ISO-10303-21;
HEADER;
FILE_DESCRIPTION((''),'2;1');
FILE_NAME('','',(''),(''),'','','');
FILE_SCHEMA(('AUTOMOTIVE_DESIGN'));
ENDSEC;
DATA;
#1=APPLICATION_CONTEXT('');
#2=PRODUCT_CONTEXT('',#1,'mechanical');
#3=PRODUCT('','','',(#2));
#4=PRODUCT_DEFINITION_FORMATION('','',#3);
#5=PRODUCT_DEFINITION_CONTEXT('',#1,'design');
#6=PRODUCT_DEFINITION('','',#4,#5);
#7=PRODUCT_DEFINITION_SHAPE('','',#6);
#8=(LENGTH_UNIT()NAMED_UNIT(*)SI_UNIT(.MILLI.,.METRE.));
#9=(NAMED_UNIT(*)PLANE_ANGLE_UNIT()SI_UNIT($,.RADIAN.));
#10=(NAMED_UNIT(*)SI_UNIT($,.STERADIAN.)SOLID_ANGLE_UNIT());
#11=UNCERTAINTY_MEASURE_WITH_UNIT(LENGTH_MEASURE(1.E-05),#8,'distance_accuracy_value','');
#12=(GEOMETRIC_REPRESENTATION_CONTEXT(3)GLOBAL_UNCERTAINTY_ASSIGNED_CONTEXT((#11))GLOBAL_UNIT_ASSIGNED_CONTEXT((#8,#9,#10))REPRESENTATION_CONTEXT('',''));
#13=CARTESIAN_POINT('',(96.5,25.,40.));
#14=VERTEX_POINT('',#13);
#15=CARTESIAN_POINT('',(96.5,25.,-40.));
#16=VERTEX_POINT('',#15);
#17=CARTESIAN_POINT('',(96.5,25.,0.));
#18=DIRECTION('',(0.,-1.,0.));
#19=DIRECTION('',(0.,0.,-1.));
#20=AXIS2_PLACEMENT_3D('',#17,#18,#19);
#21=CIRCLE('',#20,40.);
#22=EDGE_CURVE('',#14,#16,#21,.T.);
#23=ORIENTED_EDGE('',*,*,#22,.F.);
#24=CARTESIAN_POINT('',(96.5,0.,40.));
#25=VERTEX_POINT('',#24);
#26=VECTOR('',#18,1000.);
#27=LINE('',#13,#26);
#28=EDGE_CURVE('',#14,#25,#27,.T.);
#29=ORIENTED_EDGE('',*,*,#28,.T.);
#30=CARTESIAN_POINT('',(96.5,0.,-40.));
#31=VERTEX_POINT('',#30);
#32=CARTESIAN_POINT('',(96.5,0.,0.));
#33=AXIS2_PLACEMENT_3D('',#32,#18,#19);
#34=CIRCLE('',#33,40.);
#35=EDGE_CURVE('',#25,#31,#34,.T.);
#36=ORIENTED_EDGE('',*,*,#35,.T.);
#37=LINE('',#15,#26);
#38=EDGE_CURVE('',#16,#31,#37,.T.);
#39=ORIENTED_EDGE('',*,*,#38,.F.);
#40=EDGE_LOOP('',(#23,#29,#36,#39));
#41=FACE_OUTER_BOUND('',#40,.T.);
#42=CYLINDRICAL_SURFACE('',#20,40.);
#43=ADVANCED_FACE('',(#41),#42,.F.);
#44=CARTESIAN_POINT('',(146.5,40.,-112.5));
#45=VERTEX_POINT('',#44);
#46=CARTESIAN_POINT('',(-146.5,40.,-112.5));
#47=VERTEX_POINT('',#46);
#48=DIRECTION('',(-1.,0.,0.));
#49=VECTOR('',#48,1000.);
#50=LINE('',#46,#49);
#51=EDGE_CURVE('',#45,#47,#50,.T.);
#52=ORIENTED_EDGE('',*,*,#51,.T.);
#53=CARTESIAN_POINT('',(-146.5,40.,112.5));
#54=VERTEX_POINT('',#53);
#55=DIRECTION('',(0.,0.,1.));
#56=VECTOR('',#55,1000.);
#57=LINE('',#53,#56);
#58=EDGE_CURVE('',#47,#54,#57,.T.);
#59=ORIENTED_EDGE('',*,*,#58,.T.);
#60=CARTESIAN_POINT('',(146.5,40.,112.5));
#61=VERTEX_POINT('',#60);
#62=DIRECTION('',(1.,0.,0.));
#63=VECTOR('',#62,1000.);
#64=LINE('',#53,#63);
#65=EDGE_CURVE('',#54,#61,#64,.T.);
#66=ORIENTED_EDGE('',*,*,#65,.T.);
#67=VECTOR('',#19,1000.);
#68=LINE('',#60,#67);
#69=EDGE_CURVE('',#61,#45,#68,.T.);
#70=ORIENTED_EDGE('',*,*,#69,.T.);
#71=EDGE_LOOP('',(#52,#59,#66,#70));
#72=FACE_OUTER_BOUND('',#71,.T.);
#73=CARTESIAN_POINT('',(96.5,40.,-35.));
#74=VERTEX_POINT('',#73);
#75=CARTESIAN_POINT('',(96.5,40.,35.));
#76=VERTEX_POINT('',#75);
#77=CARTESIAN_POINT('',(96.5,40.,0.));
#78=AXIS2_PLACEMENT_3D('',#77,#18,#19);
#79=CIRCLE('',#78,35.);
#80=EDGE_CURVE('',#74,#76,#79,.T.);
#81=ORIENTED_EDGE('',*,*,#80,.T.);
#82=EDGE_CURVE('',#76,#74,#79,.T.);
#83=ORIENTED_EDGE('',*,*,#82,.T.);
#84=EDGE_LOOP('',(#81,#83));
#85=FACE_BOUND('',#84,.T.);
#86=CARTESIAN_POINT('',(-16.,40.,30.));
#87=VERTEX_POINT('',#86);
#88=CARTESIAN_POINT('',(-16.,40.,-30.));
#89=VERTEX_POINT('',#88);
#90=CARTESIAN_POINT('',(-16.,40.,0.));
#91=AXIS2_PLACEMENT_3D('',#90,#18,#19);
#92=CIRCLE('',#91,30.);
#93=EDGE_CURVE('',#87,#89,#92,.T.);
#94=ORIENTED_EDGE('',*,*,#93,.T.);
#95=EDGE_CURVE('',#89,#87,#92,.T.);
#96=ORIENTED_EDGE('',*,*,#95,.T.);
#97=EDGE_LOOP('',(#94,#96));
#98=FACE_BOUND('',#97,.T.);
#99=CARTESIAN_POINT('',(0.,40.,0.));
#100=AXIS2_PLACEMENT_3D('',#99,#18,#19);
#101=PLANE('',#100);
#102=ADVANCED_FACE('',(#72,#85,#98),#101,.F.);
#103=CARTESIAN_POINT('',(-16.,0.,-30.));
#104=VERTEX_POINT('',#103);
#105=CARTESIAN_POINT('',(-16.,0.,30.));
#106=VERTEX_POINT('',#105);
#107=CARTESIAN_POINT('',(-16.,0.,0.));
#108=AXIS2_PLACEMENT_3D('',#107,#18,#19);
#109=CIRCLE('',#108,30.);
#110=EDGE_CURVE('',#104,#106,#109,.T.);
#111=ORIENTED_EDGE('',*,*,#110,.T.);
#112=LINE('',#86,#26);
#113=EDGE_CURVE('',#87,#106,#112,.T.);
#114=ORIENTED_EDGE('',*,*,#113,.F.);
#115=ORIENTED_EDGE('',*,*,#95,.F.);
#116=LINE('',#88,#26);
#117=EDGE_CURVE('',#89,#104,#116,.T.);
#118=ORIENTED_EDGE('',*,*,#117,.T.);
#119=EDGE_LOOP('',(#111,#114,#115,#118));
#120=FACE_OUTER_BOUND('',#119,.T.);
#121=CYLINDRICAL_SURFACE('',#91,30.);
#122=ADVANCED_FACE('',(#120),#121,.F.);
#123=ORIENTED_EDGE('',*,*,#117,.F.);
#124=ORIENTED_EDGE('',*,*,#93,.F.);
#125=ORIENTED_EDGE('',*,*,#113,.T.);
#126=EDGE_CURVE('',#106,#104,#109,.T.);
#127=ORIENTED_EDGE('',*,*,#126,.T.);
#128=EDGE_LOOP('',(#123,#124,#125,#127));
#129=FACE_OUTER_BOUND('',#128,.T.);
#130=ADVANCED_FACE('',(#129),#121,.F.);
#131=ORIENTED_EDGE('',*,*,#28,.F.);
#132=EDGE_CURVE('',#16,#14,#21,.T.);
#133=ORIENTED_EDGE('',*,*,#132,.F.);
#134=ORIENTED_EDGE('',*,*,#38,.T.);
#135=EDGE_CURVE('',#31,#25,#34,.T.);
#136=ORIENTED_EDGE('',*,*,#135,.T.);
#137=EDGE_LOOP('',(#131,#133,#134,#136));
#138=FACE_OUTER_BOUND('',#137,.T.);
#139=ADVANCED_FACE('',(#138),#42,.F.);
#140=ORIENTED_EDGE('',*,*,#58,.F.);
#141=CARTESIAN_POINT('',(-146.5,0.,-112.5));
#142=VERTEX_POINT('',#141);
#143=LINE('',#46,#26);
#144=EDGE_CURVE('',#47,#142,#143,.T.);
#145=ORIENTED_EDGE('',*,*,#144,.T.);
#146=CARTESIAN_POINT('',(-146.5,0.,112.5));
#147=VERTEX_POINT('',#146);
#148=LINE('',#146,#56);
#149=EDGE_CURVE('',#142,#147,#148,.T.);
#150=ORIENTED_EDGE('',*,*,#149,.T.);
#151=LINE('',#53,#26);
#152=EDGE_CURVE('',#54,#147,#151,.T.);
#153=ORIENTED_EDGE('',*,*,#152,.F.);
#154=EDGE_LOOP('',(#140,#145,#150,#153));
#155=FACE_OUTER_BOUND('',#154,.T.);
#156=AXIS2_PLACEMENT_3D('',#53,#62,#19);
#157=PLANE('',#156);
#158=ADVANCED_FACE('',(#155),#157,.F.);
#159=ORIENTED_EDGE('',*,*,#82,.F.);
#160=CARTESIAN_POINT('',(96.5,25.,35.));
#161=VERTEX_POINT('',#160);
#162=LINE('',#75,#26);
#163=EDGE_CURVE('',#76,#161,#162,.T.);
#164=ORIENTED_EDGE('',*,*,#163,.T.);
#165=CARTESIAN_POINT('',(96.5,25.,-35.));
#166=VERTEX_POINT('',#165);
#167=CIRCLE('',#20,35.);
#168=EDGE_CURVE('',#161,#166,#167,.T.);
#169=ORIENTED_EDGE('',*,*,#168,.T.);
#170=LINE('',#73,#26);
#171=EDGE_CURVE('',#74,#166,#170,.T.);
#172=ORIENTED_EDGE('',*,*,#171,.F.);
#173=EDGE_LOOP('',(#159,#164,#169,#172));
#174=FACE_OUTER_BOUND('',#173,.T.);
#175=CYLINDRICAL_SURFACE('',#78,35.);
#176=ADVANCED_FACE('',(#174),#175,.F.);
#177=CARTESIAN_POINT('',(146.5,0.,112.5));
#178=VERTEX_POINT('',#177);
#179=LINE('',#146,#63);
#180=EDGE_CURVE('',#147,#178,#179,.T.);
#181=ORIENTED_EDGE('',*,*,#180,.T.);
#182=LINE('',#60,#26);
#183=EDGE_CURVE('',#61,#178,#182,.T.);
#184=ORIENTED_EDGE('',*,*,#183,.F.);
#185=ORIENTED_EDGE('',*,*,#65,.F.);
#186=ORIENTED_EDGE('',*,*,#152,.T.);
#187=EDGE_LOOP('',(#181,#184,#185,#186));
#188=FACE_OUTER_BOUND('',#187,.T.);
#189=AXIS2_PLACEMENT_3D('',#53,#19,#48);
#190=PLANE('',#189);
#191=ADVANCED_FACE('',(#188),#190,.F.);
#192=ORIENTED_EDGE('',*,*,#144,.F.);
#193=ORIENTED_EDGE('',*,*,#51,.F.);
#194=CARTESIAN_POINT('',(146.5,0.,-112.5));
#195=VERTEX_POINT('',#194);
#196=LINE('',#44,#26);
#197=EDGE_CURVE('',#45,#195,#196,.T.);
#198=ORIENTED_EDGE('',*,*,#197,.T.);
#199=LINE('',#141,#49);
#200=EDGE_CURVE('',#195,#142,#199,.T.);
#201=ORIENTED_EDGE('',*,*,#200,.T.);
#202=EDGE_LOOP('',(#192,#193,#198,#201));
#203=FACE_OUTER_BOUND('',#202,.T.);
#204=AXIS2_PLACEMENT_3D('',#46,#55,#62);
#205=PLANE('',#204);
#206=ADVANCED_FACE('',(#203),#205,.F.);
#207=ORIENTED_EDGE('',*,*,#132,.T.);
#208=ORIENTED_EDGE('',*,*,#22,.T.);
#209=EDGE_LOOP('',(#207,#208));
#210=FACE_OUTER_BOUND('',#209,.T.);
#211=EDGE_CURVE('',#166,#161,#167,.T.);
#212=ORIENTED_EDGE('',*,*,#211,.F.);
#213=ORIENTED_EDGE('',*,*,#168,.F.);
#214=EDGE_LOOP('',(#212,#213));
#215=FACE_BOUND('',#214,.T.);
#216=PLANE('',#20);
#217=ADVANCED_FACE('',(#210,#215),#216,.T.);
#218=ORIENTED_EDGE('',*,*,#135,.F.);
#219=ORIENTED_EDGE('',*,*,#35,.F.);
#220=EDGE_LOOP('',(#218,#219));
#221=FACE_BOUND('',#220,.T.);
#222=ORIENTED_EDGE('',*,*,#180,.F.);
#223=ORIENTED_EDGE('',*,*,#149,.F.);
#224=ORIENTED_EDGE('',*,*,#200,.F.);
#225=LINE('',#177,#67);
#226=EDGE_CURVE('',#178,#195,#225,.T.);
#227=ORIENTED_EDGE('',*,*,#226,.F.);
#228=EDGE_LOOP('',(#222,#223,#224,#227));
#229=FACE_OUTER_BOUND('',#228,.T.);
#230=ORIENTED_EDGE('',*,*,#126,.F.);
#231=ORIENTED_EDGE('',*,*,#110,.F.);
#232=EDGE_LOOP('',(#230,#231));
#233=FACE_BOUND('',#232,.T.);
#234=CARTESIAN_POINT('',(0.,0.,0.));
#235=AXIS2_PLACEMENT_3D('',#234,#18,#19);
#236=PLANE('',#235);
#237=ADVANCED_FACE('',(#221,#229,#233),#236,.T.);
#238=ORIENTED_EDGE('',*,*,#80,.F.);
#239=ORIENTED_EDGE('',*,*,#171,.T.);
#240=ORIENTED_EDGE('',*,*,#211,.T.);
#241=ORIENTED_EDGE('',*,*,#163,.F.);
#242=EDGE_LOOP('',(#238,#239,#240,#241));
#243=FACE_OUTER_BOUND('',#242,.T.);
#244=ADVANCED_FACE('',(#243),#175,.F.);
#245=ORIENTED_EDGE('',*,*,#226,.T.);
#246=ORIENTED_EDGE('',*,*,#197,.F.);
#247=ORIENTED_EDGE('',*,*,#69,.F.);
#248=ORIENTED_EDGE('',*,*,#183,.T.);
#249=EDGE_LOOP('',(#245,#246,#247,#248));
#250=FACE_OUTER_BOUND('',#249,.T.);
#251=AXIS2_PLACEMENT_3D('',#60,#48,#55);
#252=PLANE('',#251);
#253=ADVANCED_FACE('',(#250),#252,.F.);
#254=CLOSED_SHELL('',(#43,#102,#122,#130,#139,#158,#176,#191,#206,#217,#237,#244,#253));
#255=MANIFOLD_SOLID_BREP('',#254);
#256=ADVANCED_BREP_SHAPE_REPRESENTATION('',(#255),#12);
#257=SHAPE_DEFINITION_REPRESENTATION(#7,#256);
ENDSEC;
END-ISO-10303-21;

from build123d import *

# Parameters (mm, degrees)
SKETCH_1_W          = 293
SKETCH_1_H          = 225
EXTRUDE_1_DEPTH     = 40
SKETCH_2_R          = 40
CUT_EXTRUDE_1_DEPTH = 25
SKETCH_3_R          = 30
CUT_EXTRUDE_2_DEPTH = 189.993386128
SKETCH_4_R          = 35
CUT_EXTRUDE_3_DEPTH = 189.993386128


with BuildPart() as part:
    # 草图1 → 凸台-拉伸1 (new body)
    with BuildSketch(Plane(origin=(0, 0, 0), x_dir=(1, 0, 0), z_dir=(0, 1, 0))):
        Rectangle(SKETCH_1_W, SKETCH_1_H)
    extrude(amount=EXTRUDE_1_DEPTH)

    # 草图2 → 切除-拉伸1 (cut)
    with BuildSketch(Plane.XZ):
        with Locations(Location((96.5, 0, 0), (0, 0, 270))):
            Circle(SKETCH_2_R)
    extrude(amount=-CUT_EXTRUDE_1_DEPTH, mode=Mode.SUBTRACT)

    # 草图3 → 切除-拉伸2 (cut, through all)
    with BuildSketch(Plane.XZ):
        with Locations(Location((-16, 0, 0), (0, 0, 270))):
            Circle(SKETCH_3_R)
    extrude(amount=-CUT_EXTRUDE_2_DEPTH, mode=Mode.SUBTRACT)

    # 草图4 → 切除-拉伸3 (cut, through all)
    with BuildSketch(Plane.XZ):
        with Locations(Location((96.5, 0, 0), (0, 0, 270))):
            Circle(SKETCH_4_R)
    extrude(amount=-CUT_EXTRUDE_3_DEPTH, mode=Mode.SUBTRACT)


solid = part.part
